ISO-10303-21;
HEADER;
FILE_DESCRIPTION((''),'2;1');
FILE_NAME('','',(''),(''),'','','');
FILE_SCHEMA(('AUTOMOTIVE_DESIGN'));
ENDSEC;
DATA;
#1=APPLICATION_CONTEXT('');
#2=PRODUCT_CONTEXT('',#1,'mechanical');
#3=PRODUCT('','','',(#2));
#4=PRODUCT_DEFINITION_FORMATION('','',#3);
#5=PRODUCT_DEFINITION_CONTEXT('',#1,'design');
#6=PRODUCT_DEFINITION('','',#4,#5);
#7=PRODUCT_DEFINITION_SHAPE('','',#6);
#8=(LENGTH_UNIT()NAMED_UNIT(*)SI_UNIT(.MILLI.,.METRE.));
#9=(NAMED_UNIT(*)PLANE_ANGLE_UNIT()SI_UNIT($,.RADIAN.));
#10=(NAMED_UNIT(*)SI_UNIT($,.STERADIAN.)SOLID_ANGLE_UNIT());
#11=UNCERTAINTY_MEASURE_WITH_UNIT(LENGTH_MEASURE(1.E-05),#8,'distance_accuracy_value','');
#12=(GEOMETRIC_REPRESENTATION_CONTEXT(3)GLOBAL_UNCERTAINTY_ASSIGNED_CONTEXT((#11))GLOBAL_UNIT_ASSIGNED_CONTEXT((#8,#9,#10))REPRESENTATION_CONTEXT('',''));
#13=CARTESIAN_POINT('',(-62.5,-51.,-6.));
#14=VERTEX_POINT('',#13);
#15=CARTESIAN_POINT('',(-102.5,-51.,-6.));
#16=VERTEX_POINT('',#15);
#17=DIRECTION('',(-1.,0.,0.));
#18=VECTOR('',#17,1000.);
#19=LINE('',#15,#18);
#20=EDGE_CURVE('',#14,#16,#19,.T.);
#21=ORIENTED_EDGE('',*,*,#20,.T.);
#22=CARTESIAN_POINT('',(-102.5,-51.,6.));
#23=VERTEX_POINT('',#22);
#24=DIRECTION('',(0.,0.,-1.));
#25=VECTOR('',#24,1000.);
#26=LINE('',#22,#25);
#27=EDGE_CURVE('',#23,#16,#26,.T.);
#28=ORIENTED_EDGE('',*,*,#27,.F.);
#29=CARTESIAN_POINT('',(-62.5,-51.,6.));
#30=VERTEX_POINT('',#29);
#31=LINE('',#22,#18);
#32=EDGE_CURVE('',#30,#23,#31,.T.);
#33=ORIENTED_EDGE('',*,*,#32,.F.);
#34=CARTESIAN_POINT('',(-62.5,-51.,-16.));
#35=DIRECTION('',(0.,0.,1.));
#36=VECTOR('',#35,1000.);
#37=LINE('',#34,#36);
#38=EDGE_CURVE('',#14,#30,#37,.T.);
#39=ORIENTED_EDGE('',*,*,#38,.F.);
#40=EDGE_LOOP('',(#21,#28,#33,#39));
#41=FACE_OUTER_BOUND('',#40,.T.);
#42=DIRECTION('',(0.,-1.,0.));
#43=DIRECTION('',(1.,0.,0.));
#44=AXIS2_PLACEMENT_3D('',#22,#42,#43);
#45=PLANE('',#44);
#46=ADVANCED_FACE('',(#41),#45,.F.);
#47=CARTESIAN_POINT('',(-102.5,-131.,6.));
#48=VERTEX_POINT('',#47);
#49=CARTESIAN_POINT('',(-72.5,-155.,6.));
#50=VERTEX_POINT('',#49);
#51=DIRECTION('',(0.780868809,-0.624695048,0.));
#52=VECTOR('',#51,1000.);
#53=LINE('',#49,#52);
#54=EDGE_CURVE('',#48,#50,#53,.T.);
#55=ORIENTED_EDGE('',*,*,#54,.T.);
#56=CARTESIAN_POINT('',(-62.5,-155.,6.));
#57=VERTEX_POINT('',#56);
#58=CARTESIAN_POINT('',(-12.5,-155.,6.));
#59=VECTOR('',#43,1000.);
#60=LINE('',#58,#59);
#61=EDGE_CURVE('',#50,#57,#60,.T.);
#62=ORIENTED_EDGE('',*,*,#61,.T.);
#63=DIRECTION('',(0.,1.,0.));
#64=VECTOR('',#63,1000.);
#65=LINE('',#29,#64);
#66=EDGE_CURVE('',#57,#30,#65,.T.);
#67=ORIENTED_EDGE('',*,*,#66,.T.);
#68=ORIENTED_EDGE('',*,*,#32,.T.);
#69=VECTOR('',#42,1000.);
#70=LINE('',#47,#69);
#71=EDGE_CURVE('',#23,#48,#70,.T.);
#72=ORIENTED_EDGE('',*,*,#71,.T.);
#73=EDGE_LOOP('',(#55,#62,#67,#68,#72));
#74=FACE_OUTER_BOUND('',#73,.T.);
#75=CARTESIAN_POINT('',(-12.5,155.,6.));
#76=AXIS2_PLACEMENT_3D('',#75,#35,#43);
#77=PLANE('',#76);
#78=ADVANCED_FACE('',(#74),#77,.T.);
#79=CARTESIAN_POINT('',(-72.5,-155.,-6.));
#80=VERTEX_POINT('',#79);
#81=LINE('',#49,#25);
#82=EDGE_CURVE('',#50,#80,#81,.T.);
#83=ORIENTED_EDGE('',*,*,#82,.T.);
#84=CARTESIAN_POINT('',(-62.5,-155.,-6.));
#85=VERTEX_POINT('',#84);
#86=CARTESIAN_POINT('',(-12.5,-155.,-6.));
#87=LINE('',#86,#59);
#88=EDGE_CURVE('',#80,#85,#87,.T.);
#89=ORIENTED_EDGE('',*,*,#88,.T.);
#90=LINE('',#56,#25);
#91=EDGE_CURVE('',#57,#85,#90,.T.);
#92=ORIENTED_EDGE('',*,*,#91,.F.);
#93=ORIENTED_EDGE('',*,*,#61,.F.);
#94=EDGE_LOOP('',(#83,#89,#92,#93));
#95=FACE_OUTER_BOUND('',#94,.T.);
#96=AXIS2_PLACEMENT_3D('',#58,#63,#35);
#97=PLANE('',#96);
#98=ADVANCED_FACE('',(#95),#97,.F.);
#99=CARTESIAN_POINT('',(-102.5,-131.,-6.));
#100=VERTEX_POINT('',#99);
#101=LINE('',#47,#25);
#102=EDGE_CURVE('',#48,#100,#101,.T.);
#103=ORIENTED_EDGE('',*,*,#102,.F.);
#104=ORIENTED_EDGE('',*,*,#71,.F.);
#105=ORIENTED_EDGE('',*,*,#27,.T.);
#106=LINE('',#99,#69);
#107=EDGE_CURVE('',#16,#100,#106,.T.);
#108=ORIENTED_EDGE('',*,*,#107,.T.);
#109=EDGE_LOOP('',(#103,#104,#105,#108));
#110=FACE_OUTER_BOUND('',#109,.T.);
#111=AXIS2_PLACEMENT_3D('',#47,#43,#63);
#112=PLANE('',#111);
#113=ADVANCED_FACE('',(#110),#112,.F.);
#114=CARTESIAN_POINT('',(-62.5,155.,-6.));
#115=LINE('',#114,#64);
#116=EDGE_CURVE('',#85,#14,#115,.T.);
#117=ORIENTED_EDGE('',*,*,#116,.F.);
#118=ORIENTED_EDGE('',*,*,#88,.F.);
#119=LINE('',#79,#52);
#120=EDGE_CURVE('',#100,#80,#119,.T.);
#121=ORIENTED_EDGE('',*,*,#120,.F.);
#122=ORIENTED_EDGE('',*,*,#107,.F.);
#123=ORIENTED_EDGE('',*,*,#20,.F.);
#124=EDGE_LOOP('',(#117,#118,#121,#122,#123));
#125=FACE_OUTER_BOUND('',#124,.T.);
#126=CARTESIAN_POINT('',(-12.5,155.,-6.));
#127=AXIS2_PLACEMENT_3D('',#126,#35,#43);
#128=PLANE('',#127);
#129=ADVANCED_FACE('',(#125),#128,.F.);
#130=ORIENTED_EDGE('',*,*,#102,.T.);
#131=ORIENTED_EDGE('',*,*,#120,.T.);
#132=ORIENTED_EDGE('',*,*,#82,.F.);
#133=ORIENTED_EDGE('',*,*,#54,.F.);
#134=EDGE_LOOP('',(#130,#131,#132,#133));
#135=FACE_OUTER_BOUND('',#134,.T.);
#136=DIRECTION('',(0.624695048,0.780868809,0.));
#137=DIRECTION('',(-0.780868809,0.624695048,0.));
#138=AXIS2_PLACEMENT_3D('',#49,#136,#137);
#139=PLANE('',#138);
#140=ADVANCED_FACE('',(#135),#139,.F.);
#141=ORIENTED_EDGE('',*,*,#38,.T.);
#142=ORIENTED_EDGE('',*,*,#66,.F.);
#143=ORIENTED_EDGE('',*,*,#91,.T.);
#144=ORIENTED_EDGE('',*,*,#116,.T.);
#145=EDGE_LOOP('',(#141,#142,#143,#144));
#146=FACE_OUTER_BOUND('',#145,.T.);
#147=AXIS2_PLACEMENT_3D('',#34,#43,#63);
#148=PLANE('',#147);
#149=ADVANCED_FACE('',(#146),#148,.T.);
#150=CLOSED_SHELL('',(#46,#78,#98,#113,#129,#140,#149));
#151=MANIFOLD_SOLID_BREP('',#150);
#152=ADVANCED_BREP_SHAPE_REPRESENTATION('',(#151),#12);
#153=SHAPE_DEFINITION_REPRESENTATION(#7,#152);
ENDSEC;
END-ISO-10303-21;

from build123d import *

# Parameters (mm, degrees)
SKETCH1_W           = 25
SKETCH1_H           = 310
EXTRUDE1_DEPTH      = 6
EXTRUDE3_DEPTH      = 6
SKETCH4_OUTSIDE_W   = 183.172
SKETCH4_OUTSIDE_H   = 378.172
SKETCH4_OUTSIDE_W_2 = 40
SKETCH4_OUTSIDE_H_2 = 128.082699231
CUT_EXTRUDE1_DEPTH  = 22


with BuildPart() as part:
    # Sketch1 → Extrude1 (new, symmetric)
    with BuildSketch(Plane.XY):
        Rectangle(SKETCH1_W, SKETCH1_H)
    extrude(amount=EXTRUDE1_DEPTH, both=True)

    # Sketch3 → Extrude3 (add, symmetric)
    with BuildSketch(Plane.XY):
        Polygon((-12.5, 155), (-72.5, 155), (-102.5, 131), (-102.5, 51), (-12.5, 51), align=None)
        Polygon((-12.5, -51), (-12.5, -155), (-72.5, -155), (-102.5, -131), (-102.5, -51), align=None)
    extrude(amount=EXTRUDE3_DEPTH, both=True)

    # Sketch4 outside → Cut-Extrude1 (cut)
    with BuildSketch(Plane.XY.offset(6)):
        with Locations((-45, 0)):
            Rectangle(SKETCH4_OUTSIDE_W, SKETCH4_OUTSIDE_H)
        with Locations((-82.5, -115.041349616)):
            Rectangle(SKETCH4_OUTSIDE_W_2, SKETCH4_OUTSIDE_H_2, mode=Mode.SUBTRACT)
    extrude(amount=-CUT_EXTRUDE1_DEPTH, mode=Mode.SUBTRACT)


solid = part.part
